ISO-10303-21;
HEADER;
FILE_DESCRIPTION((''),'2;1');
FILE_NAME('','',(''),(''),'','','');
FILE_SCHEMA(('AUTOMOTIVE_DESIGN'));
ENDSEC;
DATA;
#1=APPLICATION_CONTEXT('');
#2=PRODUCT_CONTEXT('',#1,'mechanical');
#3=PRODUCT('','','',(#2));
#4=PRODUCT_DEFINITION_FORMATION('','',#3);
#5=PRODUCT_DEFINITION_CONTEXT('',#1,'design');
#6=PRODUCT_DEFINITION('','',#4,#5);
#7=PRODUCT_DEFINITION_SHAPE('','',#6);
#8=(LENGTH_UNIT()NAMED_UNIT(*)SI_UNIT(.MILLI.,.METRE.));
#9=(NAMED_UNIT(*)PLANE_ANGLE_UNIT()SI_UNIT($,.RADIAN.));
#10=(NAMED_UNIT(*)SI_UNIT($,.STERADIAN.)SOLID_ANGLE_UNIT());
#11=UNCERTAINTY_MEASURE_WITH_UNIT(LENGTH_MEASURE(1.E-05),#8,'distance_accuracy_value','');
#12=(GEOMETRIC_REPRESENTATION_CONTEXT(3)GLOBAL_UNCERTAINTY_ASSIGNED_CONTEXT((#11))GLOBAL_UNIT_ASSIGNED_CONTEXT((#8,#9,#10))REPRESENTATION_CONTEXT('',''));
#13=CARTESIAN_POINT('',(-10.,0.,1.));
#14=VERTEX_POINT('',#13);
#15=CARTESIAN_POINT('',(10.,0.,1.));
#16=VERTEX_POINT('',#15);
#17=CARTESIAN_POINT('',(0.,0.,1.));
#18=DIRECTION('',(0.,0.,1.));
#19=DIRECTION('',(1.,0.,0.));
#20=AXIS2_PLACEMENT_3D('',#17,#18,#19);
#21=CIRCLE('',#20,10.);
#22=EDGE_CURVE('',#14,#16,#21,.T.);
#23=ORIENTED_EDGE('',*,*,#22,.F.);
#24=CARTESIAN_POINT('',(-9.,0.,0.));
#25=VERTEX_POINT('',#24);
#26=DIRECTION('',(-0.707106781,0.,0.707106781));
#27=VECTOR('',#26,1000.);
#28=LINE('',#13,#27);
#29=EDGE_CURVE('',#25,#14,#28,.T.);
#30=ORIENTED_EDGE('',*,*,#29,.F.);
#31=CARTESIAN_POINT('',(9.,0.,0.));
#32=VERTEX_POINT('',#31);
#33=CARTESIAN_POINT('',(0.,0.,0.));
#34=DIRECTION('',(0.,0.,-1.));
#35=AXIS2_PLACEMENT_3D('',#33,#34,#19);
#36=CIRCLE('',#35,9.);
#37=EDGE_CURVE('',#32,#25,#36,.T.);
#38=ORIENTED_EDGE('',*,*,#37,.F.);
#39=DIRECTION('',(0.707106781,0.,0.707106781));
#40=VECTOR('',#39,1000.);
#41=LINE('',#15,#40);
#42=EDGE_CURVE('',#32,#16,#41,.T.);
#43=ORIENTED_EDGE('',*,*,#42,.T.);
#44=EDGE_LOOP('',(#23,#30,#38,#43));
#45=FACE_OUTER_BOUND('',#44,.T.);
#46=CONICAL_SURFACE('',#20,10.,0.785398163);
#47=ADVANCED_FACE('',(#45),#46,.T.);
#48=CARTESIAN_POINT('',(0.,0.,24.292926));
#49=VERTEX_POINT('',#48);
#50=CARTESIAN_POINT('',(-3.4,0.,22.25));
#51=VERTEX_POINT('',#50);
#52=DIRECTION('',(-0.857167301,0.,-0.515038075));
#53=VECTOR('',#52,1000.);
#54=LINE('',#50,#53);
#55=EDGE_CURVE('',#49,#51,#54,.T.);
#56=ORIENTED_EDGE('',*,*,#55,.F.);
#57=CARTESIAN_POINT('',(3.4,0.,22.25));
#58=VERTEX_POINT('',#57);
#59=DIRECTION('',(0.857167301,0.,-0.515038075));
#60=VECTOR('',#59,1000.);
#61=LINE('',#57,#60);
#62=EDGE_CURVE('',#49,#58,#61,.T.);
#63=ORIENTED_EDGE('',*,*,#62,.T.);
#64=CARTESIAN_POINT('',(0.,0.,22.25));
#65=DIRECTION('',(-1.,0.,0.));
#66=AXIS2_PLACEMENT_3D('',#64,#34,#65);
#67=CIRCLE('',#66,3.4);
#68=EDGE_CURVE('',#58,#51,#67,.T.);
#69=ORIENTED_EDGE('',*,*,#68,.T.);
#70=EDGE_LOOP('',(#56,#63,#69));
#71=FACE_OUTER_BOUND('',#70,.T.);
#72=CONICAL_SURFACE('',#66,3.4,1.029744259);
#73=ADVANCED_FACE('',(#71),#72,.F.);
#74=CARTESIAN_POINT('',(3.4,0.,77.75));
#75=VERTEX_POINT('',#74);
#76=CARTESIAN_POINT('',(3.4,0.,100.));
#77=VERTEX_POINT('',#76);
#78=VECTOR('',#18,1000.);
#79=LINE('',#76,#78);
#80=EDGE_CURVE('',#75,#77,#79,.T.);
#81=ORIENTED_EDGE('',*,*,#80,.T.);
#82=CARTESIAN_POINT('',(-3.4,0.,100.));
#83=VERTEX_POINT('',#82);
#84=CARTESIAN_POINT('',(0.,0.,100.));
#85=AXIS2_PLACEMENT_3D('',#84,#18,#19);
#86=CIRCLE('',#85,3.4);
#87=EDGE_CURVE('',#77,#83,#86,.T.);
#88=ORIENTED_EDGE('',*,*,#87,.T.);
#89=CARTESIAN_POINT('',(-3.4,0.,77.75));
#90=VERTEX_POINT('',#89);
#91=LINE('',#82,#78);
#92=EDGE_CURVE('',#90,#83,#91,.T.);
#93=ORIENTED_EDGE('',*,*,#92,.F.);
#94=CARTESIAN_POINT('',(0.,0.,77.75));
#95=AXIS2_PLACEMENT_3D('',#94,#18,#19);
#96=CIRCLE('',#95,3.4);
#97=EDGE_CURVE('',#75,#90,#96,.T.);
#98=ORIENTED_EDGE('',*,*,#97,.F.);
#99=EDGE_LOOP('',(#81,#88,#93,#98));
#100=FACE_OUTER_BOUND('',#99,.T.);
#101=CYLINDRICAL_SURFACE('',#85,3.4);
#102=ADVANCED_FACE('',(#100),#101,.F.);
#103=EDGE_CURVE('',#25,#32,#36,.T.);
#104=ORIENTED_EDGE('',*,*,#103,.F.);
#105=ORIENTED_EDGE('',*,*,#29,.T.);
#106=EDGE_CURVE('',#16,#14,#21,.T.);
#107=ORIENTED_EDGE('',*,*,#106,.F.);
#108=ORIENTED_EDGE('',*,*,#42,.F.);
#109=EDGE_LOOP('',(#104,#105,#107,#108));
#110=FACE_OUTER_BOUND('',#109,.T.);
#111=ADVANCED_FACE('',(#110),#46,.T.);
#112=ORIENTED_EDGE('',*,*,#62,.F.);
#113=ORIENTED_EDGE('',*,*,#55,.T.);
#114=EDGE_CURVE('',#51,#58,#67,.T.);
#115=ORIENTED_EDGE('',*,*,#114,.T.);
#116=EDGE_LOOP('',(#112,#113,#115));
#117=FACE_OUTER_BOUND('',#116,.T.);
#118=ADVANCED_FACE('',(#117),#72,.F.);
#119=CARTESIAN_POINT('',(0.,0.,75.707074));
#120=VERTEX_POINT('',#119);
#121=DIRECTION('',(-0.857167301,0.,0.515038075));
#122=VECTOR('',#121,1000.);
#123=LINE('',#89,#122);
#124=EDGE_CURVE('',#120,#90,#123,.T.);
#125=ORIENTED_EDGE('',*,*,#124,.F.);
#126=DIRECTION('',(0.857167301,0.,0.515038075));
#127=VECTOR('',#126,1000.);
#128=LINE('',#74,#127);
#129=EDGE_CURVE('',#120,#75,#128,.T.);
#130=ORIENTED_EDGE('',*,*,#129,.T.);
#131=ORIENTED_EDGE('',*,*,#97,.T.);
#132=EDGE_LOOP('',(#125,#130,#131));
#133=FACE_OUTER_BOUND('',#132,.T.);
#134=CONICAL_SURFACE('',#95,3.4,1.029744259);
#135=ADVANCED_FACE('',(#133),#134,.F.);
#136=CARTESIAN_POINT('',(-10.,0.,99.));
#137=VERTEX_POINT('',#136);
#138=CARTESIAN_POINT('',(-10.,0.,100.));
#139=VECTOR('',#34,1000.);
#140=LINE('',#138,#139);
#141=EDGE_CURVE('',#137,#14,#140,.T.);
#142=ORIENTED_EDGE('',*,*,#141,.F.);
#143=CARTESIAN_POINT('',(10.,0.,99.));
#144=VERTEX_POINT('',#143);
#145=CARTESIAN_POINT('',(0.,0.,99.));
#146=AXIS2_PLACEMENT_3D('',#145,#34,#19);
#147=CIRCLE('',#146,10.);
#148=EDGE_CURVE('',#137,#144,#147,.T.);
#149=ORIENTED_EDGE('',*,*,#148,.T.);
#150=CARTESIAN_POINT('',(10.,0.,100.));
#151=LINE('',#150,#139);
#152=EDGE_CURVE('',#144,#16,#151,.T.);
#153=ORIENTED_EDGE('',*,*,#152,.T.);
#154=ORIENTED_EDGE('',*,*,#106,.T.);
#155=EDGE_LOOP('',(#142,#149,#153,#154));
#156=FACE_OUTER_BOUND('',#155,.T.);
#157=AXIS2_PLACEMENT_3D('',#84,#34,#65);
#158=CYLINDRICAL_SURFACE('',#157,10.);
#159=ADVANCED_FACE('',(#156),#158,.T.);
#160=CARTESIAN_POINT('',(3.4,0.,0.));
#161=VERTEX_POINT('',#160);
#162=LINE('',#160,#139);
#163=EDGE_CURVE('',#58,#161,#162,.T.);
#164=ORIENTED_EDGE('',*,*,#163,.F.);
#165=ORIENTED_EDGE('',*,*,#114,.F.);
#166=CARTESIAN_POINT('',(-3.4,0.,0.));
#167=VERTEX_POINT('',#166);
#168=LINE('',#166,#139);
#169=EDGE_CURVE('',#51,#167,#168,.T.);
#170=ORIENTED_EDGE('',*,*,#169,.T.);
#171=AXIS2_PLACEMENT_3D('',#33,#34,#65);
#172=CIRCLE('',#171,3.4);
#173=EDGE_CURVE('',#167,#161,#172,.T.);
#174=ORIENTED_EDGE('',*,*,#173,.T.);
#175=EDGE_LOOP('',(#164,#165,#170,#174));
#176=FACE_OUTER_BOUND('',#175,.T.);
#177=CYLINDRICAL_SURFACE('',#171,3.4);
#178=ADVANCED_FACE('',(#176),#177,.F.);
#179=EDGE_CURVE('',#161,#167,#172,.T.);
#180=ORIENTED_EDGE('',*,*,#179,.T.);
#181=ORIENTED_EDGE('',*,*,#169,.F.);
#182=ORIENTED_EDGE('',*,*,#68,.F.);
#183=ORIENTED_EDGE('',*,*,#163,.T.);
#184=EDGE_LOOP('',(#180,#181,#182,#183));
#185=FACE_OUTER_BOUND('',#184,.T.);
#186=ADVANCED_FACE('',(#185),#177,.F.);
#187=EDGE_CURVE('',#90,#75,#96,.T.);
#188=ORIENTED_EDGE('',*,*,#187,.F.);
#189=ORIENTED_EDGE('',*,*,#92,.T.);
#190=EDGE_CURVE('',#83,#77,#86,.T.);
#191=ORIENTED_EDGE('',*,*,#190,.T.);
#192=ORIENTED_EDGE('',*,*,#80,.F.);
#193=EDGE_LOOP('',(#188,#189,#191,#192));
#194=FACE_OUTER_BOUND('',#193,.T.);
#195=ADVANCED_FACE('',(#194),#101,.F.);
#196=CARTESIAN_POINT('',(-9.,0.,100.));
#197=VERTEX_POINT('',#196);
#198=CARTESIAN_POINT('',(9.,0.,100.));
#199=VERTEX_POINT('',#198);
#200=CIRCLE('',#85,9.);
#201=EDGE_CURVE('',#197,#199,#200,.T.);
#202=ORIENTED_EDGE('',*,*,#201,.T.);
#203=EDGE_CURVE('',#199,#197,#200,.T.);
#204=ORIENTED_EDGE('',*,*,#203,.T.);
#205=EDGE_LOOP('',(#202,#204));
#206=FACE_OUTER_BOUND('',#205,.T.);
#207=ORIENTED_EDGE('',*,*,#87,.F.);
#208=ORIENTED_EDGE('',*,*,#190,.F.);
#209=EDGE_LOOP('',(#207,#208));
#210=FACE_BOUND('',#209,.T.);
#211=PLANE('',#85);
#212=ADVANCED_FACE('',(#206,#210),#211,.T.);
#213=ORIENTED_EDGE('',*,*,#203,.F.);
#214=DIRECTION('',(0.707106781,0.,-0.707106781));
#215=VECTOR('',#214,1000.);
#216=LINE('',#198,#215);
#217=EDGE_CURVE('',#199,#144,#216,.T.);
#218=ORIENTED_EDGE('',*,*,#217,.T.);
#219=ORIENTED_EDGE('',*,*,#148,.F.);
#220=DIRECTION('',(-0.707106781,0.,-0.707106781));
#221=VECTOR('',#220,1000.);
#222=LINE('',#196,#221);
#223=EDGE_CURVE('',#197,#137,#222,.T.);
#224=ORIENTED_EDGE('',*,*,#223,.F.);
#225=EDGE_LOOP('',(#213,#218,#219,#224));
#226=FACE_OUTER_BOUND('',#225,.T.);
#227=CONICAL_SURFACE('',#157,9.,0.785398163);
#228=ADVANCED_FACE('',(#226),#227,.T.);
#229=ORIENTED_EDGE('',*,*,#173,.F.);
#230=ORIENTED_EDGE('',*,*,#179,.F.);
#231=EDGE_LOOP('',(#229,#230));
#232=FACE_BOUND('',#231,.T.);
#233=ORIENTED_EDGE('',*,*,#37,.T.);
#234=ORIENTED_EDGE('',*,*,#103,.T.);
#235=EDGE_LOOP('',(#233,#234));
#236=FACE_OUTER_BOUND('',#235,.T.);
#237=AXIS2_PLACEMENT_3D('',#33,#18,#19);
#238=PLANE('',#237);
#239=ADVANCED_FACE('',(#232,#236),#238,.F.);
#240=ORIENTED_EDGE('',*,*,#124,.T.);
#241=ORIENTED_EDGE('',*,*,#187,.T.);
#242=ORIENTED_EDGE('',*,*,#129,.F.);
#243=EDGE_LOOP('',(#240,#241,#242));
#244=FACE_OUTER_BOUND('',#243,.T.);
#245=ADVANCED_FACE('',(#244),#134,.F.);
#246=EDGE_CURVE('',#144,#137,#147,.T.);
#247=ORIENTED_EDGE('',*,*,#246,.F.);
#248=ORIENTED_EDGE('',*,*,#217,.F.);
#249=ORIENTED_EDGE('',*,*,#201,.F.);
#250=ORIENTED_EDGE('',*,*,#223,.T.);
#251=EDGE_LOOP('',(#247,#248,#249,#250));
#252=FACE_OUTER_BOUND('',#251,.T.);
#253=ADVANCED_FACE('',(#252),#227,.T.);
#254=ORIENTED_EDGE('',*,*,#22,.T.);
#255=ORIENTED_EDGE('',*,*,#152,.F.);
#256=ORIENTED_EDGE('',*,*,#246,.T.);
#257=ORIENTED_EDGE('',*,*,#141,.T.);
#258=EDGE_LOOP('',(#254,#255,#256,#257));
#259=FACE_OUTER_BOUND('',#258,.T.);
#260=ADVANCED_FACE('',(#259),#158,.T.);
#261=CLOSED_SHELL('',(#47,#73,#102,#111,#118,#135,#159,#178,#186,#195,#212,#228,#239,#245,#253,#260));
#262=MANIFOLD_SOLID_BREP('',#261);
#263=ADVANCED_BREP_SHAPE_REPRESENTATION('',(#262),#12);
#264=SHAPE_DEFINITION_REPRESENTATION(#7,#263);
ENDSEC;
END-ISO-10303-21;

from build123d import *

# Parameters (mm, degrees)
SKETCH1_R             = 10
BOSS_EXTRUDE1_DEPTH   = 100
M8_TAPPED_HOLE1_D     = 6.8
M8_TAPPED_HOLE1_DEPTH = 22.25
M8_TAPPED_HOLE1_TIP   = 2.042926105
CHAMFER1_SIZE         = 1
CHAMFER3_SIZE         = 1
M8_TAPPED_HOLE2_D     = 6.8
M8_TAPPED_HOLE2_DEPTH = 22.25
M8_TAPPED_HOLE2_TIP   = 2.042926105


with BuildPart() as part:
    # Sketch1 → Boss-Extrude1 (new body)
    with BuildSketch(Plane.XY):
        Circle(SKETCH1_R)
    extrude(amount=BOSS_EXTRUDE1_DEPTH)

    # M8 Tapped Hole1
    with Locations(Plane.XY.offset(100)):
        with Locations((0, 0)):
            Hole(M8_TAPPED_HOLE1_D / 2, depth=M8_TAPPED_HOLE1_DEPTH)
            with Locations((0, 0, -(M8_TAPPED_HOLE1_DEPTH + M8_TAPPED_HOLE1_TIP / 2))):  # 118° drill point
                Cone(0, M8_TAPPED_HOLE1_D / 2, M8_TAPPED_HOLE1_TIP, mode=Mode.SUBTRACT)

    # Chamfer1
    chamfer1_edges = [part.edges().sort_by_distance(p)[0] for p in [
        (-10, 0, 100),
    ]]
    chamfer(chamfer1_edges, length=CHAMFER1_SIZE)

    # Chamfer3
    chamfer3_edges = [part.edges().sort_by_distance(p)[0] for p in [
        (-10, 0, 0),
    ]]
    chamfer(chamfer3_edges, length=CHAMFER3_SIZE)

    # M8 Tapped Hole2
    with Locations(Plane(origin=(0, 0, 0), x_dir=(-1, 0, 0), z_dir=(0, 0, -1))):
        with Locations((0, 0)):
            Hole(M8_TAPPED_HOLE2_D / 2, depth=M8_TAPPED_HOLE2_DEPTH)
            with Locations((0, 0, -(M8_TAPPED_HOLE2_DEPTH + M8_TAPPED_HOLE2_TIP / 2))):  # 118° drill point
                Cone(0, M8_TAPPED_HOLE2_D / 2, M8_TAPPED_HOLE2_TIP, mode=Mode.SUBTRACT)


solid = part.part
